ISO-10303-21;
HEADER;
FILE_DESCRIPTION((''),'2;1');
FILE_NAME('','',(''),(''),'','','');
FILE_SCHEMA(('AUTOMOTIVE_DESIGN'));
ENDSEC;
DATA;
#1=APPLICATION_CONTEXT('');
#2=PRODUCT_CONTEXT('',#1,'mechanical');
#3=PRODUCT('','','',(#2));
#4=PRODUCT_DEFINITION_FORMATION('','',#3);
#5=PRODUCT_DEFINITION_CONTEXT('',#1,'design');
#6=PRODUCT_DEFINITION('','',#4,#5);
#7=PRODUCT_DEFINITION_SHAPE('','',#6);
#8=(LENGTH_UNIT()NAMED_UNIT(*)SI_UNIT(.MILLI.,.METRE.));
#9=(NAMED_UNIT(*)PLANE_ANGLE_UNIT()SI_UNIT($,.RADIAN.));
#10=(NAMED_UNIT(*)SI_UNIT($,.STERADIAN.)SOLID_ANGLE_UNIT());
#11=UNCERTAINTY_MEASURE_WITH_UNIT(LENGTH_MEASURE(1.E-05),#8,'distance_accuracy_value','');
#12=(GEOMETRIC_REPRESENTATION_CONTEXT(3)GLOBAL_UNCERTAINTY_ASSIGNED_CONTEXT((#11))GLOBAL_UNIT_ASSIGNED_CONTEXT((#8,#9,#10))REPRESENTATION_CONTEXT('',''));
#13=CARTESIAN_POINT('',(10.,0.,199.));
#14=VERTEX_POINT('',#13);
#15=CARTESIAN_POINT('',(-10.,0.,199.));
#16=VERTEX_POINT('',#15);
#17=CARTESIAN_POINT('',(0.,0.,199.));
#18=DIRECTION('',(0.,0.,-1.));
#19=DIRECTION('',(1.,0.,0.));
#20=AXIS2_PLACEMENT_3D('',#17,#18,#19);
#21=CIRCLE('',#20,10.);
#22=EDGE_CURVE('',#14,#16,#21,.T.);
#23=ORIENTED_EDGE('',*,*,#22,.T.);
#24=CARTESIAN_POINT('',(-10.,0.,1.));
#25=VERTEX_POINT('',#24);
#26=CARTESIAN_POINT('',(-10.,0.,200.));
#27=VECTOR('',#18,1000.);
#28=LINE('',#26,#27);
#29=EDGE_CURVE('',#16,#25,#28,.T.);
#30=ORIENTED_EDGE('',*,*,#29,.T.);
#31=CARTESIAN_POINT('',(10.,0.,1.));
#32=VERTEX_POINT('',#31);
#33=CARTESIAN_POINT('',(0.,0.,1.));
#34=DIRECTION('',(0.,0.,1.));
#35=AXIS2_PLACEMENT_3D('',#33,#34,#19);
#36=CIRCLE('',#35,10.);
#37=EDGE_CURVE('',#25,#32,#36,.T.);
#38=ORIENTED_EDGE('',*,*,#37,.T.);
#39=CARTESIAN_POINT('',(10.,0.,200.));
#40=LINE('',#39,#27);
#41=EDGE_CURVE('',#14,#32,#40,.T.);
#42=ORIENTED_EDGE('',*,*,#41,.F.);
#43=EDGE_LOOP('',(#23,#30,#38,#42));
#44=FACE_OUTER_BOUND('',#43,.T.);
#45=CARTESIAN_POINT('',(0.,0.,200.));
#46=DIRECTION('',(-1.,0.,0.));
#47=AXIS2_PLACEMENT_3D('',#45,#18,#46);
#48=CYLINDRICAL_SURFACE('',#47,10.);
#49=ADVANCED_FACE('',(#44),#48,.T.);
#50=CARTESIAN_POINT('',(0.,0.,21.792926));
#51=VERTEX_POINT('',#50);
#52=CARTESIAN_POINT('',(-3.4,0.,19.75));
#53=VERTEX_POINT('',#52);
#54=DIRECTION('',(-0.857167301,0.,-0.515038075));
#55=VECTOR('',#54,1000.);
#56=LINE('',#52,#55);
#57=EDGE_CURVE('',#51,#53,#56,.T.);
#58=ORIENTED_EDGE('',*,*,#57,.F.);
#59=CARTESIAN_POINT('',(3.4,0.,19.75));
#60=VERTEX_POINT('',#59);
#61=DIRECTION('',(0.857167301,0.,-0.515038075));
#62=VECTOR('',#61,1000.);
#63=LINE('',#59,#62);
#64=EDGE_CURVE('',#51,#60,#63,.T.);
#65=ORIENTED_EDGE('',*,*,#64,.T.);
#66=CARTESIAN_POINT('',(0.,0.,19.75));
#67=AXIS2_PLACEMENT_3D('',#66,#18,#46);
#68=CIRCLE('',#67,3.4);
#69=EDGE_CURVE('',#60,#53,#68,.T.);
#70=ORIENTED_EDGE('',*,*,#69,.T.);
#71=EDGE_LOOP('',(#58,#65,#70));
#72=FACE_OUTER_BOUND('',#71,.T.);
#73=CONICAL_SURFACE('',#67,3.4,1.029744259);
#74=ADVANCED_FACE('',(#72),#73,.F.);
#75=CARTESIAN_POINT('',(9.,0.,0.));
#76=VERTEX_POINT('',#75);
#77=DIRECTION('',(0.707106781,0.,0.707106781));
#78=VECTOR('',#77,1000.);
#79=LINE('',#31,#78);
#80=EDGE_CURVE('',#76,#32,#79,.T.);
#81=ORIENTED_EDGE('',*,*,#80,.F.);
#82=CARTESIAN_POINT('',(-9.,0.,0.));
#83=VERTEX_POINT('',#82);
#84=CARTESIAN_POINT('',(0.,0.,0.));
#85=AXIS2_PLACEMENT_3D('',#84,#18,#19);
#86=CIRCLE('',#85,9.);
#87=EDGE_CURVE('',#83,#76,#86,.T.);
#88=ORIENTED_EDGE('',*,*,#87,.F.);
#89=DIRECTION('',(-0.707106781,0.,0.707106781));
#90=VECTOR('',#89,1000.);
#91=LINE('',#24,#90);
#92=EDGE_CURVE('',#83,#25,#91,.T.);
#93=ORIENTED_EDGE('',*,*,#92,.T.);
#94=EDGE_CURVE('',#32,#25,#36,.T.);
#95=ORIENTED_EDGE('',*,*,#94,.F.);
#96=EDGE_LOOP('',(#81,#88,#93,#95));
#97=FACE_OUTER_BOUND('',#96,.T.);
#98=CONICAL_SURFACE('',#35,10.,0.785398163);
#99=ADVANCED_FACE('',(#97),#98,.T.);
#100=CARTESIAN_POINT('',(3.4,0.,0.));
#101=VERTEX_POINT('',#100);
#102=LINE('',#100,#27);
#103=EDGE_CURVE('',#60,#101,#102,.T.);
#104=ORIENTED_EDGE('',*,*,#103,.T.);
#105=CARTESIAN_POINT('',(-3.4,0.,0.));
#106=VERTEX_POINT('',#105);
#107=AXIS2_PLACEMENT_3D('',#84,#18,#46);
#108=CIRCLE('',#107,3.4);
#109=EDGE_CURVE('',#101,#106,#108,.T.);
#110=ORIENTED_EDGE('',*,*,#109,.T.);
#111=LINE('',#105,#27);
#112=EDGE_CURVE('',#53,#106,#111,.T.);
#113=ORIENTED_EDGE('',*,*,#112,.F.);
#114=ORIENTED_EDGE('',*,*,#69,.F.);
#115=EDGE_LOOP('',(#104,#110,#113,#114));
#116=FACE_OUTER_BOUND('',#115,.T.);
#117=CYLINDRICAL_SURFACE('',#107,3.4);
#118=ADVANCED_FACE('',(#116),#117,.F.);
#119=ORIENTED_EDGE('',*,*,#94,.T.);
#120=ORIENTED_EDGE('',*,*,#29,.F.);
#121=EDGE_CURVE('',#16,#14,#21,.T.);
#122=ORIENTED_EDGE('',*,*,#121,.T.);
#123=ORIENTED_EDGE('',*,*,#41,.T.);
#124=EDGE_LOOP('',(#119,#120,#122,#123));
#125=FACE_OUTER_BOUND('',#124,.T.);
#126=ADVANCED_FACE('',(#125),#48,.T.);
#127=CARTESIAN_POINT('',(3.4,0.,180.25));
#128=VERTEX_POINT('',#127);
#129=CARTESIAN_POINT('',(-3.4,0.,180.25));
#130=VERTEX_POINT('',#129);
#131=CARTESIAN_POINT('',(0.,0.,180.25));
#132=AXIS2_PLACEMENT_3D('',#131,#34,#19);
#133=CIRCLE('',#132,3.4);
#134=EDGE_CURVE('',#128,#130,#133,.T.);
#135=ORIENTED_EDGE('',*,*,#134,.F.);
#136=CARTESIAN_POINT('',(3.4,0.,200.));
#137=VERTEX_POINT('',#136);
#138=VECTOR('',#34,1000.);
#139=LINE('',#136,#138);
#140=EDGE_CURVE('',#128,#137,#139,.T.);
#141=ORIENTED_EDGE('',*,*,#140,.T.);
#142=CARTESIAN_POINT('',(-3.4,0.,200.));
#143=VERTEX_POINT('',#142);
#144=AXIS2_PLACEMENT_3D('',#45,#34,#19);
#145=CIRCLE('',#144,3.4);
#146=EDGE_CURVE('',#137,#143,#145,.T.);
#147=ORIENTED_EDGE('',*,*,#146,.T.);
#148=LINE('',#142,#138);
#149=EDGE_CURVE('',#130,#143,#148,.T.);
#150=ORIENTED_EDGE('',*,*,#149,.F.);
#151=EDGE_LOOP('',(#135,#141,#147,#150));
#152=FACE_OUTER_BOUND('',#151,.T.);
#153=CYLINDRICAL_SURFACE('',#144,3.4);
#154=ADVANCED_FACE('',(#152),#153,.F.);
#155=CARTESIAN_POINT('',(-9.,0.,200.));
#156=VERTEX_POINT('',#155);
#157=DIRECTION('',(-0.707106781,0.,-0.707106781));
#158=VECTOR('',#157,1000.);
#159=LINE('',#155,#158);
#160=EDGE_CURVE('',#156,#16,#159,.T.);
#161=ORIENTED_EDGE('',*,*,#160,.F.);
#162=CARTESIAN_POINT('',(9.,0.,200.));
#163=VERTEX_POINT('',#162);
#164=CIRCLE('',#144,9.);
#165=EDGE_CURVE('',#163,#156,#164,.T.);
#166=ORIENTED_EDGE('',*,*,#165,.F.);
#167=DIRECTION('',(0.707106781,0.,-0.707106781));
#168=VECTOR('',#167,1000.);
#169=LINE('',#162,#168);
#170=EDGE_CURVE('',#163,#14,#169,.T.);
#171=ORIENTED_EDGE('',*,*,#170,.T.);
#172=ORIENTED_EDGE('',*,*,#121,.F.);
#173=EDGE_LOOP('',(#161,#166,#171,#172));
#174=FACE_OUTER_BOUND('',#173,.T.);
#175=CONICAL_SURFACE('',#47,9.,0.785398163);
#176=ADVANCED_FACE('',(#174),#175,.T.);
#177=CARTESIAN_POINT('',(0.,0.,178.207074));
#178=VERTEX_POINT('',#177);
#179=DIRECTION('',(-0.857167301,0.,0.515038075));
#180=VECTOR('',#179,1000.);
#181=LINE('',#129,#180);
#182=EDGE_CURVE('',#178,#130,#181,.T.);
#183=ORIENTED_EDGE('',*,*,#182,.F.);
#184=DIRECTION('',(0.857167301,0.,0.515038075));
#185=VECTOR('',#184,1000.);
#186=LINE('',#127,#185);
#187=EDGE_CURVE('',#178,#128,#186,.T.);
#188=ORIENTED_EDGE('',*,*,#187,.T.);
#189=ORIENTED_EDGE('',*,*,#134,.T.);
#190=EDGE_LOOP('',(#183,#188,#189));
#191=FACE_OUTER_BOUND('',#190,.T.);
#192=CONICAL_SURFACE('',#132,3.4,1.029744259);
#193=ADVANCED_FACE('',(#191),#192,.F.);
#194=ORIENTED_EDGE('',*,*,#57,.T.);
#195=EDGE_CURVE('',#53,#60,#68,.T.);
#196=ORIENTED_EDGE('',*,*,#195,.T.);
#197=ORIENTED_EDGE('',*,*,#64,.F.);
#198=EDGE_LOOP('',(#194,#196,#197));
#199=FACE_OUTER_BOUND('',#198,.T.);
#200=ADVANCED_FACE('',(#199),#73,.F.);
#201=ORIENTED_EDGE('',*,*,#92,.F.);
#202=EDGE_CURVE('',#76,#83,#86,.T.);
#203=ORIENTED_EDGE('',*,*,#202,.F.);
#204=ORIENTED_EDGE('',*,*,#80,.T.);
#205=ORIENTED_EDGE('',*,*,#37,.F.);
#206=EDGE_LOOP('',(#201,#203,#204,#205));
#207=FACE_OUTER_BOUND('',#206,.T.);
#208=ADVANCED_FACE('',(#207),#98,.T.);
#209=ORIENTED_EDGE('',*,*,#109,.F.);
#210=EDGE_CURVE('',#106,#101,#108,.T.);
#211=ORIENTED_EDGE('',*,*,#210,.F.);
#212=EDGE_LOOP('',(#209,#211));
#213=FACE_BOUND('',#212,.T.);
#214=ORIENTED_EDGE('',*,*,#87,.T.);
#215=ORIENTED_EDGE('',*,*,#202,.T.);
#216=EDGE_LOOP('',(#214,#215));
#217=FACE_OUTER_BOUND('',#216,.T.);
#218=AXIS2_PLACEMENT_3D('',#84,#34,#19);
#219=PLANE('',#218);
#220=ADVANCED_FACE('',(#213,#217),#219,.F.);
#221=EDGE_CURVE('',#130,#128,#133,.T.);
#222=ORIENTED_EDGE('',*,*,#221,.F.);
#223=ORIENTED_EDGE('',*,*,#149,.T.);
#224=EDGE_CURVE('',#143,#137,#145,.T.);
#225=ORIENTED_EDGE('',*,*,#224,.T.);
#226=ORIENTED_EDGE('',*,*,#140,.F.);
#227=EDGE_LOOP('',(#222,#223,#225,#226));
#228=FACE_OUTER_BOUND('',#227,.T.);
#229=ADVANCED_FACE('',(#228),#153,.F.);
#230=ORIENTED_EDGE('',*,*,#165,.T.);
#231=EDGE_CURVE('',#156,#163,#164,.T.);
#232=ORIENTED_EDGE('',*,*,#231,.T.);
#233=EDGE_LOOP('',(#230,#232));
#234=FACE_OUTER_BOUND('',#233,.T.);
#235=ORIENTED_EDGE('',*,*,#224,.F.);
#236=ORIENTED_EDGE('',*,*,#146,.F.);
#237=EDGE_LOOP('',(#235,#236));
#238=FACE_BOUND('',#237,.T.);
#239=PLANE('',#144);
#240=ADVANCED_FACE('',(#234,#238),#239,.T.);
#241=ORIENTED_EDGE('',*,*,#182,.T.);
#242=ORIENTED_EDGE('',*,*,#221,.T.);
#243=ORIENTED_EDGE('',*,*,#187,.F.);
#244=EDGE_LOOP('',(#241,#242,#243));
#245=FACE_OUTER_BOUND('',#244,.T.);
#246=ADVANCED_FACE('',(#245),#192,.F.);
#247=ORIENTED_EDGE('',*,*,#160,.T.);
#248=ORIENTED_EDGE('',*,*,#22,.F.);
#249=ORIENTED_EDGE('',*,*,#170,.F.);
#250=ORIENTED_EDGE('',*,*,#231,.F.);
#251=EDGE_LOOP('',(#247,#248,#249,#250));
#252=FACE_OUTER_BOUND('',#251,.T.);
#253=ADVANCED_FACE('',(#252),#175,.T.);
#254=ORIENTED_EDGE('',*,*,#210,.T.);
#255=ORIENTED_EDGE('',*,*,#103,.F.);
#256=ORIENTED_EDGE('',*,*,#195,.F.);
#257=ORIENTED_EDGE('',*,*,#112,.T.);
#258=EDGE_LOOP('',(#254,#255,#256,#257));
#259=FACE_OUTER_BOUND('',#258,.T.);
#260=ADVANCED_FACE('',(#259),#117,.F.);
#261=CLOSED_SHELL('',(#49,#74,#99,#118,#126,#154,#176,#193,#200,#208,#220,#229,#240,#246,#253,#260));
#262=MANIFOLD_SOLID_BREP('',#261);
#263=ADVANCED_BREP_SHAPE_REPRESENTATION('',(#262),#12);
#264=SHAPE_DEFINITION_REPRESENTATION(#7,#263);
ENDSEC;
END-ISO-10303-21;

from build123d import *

# Parameters (mm, degrees)
SKETCH_1_R             = 10
EXTRUDE_1_DEPTH        = 200
HOLE_WIZARD_M8_1_D     = 6.8
HOLE_WIZARD_M8_1_DEPTH = 19.75
HOLE_WIZARD_M8_1_TIP   = 2.042926105
HOLE_WIZARD_M8_2_D     = 6.8
HOLE_WIZARD_M8_2_DEPTH = 19.75
HOLE_WIZARD_M8_2_TIP   = 2.042926105
CHAMFER_1_SIZE         = 1


with BuildPart() as part:
    # 草图1 → 凸台-拉伸1 (new body)
    with BuildSketch(Plane.XY):
        Circle(SKETCH_1_R)
    extrude(amount=EXTRUDE_1_DEPTH)

    # M8 螺纹孔1
    with Locations(Plane(origin=(0, 0, 0), x_dir=(-1, 0, 0), z_dir=(0, 0, -1))):
        with Locations((0, 0)):
            Hole(HOLE_WIZARD_M8_1_D / 2, depth=HOLE_WIZARD_M8_1_DEPTH)
            with Locations((0, 0, -(HOLE_WIZARD_M8_1_DEPTH + HOLE_WIZARD_M8_1_TIP / 2))):  # 118° drill point
                Cone(0, HOLE_WIZARD_M8_1_D / 2, HOLE_WIZARD_M8_1_TIP, mode=Mode.SUBTRACT)

    # M8 螺纹孔2
    with Locations(Plane.XY.offset(200)):
        with Locations((0, 0)):
            Hole(HOLE_WIZARD_M8_2_D / 2, depth=HOLE_WIZARD_M8_2_DEPTH)
            with Locations((0, 0, -(HOLE_WIZARD_M8_2_DEPTH + HOLE_WIZARD_M8_2_TIP / 2))):  # 118° drill point
                Cone(0, HOLE_WIZARD_M8_2_D / 2, HOLE_WIZARD_M8_2_TIP, mode=Mode.SUBTRACT)

    # 倒角1
    chamfer_1_edges = [part.edges().sort_by_distance(p)[0] for p in [
        (-10, 0, 0),
        (-10, 0, 200),
    ]]
    chamfer(chamfer_1_edges, length=CHAMFER_1_SIZE)


solid = part.part
